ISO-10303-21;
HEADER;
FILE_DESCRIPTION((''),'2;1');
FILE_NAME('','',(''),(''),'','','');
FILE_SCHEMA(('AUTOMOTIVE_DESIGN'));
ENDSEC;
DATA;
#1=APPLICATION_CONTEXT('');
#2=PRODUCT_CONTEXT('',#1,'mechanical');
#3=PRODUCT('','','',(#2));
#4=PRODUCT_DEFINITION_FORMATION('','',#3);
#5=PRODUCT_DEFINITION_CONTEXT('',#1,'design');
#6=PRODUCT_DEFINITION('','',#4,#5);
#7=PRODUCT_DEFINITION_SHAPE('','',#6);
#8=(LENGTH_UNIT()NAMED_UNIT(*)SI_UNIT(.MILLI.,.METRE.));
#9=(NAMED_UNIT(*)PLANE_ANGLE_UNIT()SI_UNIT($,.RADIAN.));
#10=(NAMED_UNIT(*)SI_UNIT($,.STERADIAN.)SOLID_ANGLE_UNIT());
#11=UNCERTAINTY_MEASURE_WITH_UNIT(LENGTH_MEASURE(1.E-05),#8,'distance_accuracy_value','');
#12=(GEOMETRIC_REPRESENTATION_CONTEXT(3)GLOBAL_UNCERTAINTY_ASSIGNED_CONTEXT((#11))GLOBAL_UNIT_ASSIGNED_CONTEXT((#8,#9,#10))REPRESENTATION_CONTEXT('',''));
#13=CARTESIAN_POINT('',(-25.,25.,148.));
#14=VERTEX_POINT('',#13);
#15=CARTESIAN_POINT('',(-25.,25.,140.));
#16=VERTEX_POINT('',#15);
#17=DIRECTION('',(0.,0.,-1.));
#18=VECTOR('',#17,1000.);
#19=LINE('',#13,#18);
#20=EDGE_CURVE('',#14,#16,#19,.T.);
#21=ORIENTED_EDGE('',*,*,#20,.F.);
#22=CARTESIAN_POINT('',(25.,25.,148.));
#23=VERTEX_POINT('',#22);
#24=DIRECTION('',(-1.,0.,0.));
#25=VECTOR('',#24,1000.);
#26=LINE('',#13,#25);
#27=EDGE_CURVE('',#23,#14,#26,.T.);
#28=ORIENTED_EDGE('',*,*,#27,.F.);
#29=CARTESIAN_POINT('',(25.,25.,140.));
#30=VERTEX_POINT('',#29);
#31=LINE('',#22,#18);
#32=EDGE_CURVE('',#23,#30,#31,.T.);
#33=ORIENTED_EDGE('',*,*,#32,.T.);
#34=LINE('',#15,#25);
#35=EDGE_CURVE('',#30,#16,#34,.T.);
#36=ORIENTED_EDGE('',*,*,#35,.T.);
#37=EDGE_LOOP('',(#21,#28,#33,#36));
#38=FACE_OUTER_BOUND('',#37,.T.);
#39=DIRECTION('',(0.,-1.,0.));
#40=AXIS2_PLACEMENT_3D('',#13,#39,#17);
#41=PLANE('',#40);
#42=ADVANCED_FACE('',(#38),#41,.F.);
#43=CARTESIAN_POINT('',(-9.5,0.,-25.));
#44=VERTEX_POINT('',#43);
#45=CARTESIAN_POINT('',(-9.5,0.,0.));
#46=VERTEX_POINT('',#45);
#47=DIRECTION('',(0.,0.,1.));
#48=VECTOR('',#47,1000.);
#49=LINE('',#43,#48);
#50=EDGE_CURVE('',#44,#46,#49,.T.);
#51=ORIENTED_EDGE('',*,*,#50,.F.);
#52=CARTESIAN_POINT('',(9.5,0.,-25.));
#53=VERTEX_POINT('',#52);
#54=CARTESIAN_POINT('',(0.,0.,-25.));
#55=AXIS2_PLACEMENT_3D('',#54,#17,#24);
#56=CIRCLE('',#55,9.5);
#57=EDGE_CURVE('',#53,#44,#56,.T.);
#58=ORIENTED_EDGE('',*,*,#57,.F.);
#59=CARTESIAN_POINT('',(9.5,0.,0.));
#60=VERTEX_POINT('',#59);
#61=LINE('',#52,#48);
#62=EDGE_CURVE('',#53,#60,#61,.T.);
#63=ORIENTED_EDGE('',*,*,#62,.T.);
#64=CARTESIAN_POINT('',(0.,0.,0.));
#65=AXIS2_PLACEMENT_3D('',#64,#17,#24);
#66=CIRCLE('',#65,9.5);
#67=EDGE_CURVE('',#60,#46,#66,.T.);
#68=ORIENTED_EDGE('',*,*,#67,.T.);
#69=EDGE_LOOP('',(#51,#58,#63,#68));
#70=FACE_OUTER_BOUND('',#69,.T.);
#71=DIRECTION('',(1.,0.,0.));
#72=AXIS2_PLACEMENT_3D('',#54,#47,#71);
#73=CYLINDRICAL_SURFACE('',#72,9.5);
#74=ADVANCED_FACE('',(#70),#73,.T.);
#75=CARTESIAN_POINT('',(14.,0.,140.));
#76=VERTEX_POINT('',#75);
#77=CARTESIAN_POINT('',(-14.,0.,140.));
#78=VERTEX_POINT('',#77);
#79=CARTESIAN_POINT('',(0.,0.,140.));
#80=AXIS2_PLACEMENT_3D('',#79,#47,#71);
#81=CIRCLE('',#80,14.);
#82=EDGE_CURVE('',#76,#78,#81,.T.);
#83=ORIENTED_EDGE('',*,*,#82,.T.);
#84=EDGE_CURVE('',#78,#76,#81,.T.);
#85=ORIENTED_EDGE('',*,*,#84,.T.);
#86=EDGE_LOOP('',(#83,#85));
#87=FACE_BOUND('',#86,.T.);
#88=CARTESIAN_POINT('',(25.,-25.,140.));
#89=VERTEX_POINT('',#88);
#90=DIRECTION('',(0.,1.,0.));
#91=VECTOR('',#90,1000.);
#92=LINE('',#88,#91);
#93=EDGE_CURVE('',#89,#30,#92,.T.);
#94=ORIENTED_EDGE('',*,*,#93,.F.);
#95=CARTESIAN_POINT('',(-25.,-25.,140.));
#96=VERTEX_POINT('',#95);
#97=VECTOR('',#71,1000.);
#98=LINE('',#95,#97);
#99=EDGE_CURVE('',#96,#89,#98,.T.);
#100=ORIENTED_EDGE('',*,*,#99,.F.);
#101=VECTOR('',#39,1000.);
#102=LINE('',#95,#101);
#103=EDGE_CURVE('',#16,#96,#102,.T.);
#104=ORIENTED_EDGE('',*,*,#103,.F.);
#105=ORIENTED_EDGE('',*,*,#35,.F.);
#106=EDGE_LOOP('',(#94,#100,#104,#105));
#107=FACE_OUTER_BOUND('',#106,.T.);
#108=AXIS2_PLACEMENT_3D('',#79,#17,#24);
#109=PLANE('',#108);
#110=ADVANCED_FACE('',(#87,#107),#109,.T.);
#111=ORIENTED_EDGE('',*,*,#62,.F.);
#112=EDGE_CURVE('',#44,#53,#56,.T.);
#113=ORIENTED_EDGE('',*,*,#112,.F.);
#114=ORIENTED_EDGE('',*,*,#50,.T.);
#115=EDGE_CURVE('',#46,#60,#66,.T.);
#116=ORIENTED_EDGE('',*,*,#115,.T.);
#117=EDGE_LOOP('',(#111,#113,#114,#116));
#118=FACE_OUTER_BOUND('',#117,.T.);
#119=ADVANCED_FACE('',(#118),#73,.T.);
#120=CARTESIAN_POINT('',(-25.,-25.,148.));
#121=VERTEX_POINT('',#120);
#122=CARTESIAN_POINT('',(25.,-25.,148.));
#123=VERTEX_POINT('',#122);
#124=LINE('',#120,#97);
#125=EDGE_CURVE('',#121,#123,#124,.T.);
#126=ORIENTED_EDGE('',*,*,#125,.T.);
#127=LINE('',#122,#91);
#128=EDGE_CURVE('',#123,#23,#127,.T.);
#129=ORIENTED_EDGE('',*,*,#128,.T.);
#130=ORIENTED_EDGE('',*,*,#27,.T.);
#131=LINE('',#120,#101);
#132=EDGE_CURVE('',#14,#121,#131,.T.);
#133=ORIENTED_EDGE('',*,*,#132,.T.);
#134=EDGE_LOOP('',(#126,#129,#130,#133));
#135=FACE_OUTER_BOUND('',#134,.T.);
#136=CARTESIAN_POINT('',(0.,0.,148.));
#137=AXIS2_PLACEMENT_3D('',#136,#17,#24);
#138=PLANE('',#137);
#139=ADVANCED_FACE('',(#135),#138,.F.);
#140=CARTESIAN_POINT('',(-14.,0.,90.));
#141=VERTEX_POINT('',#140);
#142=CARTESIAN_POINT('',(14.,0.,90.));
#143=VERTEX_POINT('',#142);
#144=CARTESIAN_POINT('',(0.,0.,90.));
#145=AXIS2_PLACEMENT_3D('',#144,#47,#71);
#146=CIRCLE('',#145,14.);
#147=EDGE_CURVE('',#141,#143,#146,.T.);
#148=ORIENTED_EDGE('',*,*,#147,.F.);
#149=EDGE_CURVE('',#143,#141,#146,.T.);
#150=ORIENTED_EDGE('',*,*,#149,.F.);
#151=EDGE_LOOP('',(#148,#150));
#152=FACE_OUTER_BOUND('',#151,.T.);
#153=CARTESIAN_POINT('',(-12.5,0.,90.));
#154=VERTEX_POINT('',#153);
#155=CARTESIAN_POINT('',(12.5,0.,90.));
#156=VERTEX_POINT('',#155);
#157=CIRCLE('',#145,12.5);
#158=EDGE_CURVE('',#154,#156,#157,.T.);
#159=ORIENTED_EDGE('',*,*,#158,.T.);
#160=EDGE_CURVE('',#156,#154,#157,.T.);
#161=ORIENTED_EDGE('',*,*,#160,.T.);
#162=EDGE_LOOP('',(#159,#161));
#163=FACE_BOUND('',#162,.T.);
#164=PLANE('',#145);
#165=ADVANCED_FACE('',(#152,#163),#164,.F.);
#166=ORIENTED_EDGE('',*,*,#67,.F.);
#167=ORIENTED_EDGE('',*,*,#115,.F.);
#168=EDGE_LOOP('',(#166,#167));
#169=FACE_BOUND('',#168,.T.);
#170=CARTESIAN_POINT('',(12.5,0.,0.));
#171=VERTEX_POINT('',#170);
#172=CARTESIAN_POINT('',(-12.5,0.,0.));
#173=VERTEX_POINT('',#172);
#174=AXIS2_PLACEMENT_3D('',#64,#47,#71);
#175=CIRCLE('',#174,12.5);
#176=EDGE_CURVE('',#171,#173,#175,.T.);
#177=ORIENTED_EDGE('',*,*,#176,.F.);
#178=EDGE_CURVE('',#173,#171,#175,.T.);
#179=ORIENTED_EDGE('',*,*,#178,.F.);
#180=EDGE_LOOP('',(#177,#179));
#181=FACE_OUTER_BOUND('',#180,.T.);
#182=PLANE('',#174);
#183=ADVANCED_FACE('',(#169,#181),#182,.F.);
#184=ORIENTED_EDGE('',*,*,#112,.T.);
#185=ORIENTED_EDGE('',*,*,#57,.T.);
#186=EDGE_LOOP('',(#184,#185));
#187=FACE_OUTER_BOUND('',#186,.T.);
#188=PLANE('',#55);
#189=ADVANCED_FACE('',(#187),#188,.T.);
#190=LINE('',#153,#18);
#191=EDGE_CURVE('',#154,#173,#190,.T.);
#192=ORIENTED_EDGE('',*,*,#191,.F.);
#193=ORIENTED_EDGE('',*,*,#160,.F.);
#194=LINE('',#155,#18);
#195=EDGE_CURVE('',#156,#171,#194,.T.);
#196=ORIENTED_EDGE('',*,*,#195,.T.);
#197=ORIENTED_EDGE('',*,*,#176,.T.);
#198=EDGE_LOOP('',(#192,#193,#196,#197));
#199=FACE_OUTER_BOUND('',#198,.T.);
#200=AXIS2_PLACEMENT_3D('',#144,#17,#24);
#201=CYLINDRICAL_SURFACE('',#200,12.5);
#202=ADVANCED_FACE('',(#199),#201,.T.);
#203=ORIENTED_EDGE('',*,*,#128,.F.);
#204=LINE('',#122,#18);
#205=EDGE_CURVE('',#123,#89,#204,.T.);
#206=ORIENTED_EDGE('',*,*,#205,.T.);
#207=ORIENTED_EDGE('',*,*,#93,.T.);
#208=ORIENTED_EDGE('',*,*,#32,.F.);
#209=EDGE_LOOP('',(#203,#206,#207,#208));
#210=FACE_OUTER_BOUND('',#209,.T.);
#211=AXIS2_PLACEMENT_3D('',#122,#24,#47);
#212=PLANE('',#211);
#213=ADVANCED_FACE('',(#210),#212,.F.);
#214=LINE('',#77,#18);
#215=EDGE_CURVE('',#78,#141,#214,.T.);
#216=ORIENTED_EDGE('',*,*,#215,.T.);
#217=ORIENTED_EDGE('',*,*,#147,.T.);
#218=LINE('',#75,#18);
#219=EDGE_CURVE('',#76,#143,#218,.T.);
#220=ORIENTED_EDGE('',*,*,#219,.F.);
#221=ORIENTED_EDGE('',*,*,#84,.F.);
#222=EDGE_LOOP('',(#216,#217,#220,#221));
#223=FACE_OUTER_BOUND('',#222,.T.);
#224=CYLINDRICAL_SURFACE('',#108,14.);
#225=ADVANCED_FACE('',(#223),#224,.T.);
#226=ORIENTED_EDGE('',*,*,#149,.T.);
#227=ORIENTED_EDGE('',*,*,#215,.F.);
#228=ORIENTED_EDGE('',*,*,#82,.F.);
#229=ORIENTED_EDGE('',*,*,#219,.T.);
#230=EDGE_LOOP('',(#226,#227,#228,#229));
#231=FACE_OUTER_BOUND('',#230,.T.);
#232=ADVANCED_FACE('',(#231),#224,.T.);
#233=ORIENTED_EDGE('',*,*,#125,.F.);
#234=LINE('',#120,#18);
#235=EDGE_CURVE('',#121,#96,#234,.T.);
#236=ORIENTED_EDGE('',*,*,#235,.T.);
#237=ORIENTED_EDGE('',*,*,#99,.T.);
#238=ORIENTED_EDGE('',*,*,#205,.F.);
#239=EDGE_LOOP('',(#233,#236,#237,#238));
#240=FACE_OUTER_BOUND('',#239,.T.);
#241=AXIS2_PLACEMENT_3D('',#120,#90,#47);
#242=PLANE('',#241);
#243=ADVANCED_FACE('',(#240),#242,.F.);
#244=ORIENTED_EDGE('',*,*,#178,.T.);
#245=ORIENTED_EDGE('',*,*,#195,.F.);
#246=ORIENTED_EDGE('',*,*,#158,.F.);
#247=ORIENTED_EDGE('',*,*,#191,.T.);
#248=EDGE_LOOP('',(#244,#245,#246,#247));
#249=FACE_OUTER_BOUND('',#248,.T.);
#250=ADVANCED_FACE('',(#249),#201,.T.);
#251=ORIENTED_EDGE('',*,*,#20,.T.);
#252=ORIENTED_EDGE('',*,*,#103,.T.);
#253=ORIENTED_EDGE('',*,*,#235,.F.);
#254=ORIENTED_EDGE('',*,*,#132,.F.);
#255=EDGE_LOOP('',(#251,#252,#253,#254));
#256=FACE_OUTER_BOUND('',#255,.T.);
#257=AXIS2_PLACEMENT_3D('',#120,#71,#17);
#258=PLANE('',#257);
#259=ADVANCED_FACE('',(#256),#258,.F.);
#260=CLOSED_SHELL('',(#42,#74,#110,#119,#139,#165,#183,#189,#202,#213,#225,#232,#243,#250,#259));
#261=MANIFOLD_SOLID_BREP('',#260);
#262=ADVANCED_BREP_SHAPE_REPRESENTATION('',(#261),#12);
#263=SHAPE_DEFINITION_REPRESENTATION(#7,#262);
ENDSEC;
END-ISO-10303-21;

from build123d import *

# Parameters (mm, degrees)
SKETCH_1_R      = 12.5
EXTRUDE_1_DEPTH = 90
SKETCH_2_R      = 14
EXTRUDE_2_DEPTH = 50
SKETCH_3_W      = 50
SKETCH_3_H      = 50
EXTRUDE_3_DEPTH = 8
SKETCH_4_R      = 9.5
EXTRUDE_4_DEPTH = 25


with BuildPart() as part:
    # 草图1 → 凸台-拉伸1 (new body)
    with BuildSketch(Plane.XY):
        with Locations(Location((0, 0, 0), (0, 0, 180))):
            Circle(SKETCH_1_R)
    extrude(amount=EXTRUDE_1_DEPTH)

    # 草图2 → 凸台-拉伸2 (add)
    with BuildSketch(Plane.XY.offset(90)):
        Circle(SKETCH_2_R)
    extrude(amount=EXTRUDE_2_DEPTH)

    # 草图3 → 凸台-拉伸3 (add)
    with BuildSketch(Plane.XY.offset(140)):
        Rectangle(SKETCH_3_W, SKETCH_3_H)
    extrude(amount=EXTRUDE_3_DEPTH)

    # 草图4 → 凸台-拉伸4 (add)
    with BuildSketch(Plane(origin=(0, 0, 0), x_dir=(-1, 0, 0), z_dir=(0, 0, -1))):
        Circle(SKETCH_4_R)
    extrude(amount=EXTRUDE_4_DEPTH)


solid = part.part
